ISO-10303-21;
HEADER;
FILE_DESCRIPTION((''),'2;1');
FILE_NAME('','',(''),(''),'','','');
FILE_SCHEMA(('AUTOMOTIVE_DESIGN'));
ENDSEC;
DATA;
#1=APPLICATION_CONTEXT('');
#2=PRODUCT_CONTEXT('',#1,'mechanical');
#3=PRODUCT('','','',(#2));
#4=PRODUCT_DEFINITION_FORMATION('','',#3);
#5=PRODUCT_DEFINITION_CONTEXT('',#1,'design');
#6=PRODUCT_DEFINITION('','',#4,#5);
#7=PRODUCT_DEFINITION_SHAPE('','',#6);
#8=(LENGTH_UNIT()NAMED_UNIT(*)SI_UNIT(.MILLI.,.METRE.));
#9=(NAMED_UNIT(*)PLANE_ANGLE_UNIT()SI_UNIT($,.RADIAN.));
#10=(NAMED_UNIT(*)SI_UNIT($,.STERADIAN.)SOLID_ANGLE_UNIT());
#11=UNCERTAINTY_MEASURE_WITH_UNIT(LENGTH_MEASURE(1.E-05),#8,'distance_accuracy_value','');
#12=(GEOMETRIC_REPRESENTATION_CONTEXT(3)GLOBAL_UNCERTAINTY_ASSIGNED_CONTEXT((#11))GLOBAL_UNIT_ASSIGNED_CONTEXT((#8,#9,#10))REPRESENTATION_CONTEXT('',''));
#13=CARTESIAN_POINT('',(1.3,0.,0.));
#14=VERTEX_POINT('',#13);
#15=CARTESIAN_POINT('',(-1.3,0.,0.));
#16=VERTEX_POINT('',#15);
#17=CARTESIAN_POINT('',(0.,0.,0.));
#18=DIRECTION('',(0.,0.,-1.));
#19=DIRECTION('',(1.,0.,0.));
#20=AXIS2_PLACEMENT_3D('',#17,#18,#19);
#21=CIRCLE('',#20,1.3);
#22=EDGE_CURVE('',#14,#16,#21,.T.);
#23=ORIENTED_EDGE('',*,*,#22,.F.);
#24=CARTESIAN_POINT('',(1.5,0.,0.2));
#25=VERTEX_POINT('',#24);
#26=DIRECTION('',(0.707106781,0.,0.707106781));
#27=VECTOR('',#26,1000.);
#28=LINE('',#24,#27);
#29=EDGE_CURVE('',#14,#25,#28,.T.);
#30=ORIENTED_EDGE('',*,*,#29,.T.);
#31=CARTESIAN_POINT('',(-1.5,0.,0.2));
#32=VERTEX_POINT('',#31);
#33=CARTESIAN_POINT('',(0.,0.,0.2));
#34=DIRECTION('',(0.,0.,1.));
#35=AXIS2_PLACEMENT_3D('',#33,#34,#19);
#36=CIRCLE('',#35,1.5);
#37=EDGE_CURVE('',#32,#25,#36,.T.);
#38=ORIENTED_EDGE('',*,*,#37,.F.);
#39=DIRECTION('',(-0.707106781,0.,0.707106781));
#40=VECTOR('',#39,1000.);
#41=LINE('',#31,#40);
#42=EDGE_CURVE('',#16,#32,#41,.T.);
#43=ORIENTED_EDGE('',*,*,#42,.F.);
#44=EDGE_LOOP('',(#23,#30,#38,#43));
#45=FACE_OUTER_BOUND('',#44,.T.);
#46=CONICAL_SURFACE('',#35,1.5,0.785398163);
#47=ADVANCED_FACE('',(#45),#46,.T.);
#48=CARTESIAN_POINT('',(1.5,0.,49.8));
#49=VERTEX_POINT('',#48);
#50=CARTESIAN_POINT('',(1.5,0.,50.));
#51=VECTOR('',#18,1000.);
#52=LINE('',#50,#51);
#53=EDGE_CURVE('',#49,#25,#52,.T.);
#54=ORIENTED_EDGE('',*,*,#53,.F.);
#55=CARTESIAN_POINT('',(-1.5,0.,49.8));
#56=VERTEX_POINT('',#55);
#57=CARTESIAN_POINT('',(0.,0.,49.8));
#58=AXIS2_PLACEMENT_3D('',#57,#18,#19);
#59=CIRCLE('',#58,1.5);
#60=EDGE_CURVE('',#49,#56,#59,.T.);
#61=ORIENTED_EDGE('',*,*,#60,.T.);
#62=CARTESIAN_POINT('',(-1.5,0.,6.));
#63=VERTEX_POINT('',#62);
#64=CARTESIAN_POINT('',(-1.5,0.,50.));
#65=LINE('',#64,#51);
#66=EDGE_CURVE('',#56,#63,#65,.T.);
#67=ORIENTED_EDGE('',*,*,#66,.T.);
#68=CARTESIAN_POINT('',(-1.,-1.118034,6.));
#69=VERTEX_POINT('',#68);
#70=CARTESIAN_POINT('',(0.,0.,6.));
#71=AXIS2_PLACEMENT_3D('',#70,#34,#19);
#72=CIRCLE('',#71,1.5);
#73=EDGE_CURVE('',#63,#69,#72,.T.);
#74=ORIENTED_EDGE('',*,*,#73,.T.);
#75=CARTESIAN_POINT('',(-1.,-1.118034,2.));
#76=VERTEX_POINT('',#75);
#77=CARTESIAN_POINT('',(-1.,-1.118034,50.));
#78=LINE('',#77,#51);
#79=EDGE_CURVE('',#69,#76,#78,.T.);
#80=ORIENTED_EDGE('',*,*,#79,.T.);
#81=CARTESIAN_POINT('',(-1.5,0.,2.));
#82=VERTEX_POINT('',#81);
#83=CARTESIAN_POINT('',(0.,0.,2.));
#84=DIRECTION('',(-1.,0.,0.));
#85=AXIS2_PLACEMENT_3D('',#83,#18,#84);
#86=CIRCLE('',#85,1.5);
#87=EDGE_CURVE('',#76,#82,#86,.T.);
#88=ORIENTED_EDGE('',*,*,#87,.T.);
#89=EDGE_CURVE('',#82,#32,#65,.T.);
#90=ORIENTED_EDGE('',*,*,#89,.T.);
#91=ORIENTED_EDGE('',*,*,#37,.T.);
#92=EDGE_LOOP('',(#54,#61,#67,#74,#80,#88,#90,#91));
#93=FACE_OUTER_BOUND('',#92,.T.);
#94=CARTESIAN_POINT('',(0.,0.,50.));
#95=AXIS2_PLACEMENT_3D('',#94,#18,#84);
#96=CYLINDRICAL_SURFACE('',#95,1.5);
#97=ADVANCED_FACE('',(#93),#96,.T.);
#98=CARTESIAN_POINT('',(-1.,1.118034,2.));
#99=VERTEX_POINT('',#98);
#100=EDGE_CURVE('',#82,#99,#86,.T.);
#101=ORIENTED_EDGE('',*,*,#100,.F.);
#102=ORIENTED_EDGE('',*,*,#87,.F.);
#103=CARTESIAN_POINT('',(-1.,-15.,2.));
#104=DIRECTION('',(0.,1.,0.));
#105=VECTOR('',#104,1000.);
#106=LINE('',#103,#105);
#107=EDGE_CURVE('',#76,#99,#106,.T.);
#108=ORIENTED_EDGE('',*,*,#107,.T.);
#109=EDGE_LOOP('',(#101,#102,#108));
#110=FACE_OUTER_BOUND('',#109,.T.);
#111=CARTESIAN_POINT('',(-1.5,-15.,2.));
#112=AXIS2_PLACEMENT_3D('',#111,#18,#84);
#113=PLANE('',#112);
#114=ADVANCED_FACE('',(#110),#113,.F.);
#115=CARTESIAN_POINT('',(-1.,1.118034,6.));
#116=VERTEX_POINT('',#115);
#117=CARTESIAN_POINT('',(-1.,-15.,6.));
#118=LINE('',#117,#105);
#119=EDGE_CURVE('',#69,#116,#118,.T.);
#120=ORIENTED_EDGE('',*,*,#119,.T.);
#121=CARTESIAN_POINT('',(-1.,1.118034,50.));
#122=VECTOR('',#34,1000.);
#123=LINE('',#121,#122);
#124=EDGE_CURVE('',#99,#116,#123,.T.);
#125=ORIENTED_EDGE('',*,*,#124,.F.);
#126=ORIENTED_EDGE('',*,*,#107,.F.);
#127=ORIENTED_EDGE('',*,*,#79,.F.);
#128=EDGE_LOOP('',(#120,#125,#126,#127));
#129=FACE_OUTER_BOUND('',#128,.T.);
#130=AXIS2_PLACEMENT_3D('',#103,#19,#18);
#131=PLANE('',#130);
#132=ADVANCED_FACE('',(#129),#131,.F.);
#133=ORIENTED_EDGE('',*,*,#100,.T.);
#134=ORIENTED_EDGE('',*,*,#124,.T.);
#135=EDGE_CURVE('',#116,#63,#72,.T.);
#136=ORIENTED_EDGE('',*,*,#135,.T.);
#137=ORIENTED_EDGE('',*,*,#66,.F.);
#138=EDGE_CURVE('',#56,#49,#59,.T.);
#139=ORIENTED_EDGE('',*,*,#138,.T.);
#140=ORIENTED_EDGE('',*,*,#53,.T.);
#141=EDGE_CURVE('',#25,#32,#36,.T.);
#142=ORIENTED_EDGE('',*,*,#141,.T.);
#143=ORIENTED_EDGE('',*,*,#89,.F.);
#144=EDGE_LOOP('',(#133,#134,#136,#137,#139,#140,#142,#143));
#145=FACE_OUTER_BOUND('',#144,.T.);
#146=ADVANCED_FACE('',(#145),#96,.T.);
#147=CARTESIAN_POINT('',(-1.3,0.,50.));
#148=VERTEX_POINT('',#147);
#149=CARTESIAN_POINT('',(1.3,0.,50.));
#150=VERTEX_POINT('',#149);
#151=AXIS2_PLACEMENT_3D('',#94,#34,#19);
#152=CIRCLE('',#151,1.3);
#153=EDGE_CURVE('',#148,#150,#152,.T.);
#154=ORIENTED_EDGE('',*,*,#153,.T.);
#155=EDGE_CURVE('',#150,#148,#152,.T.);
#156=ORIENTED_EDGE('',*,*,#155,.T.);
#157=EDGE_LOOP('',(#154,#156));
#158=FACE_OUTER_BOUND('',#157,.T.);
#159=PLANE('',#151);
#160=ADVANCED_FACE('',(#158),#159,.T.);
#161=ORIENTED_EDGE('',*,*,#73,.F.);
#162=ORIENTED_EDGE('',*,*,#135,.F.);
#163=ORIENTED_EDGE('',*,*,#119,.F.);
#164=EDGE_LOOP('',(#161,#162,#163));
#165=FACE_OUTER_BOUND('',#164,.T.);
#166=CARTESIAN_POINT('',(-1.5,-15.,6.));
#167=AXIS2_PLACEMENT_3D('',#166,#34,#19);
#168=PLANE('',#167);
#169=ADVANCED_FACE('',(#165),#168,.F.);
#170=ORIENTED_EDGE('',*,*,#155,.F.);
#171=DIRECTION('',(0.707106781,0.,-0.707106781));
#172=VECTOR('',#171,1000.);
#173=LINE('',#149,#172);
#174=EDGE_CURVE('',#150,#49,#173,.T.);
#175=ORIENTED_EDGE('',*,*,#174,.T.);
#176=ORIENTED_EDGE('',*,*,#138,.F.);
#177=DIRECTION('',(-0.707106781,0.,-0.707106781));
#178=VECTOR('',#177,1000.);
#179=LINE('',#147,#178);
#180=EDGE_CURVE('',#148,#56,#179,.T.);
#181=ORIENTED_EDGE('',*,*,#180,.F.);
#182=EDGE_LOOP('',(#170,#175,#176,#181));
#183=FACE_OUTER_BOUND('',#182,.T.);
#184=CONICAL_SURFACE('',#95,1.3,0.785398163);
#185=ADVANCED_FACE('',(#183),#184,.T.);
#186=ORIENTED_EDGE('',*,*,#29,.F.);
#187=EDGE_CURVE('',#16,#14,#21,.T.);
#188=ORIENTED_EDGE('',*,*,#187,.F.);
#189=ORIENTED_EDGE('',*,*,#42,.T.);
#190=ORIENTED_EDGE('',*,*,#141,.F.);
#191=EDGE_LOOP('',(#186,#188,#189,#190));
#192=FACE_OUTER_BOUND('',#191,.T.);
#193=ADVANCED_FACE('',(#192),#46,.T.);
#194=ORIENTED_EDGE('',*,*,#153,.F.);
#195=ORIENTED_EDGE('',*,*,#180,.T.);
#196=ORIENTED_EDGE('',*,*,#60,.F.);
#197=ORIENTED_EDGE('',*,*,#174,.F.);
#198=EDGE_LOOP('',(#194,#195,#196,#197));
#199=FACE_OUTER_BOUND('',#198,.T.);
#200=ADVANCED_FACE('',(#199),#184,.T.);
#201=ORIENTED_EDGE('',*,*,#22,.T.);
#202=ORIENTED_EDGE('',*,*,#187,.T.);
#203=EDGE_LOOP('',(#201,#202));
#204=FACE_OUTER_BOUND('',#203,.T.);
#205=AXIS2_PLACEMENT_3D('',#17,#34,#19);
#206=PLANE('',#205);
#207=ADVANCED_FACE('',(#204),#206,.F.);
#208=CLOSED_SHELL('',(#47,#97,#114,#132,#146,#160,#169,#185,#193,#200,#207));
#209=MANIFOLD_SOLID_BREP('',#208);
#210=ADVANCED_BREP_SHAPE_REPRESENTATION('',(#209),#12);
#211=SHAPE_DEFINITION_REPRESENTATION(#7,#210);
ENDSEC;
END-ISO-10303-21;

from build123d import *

# Parameters (mm, degrees)
SKETCH1_R           = 1.5
BOSS_EXTRUDE1_DEPTH = 50
SKETCH2_W           = 0.5
SKETCH2_H           = 4
CUT_EXTRUDE1_DEPTH  = 15
CHAMFER1_SIZE       = 0.2


with BuildPart() as part:
    # Sketch1 → Boss-Extrude1 (new body)
    with BuildSketch(Plane.XY):
        Circle(SKETCH1_R)
    extrude(amount=BOSS_EXTRUDE1_DEPTH)

    # Sketch2 → Cut-Extrude1 (cut, symmetric)
    with BuildSketch(Plane(origin=(0, 0, 0), x_dir=(1, 0, 0), z_dir=(0, 1, 0))):
        with Locations((-1.25, -4)):
            Rectangle(SKETCH2_W, SKETCH2_H)
    extrude(amount=CUT_EXTRUDE1_DEPTH, both=True, mode=Mode.SUBTRACT)

    # Chamfer1
    chamfer1_edges = [part.edges().sort_by_distance(p)[0] for p in [
        (-1.5, 0, 0),
        (-1.5, 0, 50),
    ]]
    chamfer(chamfer1_edges, length=CHAMFER1_SIZE)


solid = part.part
